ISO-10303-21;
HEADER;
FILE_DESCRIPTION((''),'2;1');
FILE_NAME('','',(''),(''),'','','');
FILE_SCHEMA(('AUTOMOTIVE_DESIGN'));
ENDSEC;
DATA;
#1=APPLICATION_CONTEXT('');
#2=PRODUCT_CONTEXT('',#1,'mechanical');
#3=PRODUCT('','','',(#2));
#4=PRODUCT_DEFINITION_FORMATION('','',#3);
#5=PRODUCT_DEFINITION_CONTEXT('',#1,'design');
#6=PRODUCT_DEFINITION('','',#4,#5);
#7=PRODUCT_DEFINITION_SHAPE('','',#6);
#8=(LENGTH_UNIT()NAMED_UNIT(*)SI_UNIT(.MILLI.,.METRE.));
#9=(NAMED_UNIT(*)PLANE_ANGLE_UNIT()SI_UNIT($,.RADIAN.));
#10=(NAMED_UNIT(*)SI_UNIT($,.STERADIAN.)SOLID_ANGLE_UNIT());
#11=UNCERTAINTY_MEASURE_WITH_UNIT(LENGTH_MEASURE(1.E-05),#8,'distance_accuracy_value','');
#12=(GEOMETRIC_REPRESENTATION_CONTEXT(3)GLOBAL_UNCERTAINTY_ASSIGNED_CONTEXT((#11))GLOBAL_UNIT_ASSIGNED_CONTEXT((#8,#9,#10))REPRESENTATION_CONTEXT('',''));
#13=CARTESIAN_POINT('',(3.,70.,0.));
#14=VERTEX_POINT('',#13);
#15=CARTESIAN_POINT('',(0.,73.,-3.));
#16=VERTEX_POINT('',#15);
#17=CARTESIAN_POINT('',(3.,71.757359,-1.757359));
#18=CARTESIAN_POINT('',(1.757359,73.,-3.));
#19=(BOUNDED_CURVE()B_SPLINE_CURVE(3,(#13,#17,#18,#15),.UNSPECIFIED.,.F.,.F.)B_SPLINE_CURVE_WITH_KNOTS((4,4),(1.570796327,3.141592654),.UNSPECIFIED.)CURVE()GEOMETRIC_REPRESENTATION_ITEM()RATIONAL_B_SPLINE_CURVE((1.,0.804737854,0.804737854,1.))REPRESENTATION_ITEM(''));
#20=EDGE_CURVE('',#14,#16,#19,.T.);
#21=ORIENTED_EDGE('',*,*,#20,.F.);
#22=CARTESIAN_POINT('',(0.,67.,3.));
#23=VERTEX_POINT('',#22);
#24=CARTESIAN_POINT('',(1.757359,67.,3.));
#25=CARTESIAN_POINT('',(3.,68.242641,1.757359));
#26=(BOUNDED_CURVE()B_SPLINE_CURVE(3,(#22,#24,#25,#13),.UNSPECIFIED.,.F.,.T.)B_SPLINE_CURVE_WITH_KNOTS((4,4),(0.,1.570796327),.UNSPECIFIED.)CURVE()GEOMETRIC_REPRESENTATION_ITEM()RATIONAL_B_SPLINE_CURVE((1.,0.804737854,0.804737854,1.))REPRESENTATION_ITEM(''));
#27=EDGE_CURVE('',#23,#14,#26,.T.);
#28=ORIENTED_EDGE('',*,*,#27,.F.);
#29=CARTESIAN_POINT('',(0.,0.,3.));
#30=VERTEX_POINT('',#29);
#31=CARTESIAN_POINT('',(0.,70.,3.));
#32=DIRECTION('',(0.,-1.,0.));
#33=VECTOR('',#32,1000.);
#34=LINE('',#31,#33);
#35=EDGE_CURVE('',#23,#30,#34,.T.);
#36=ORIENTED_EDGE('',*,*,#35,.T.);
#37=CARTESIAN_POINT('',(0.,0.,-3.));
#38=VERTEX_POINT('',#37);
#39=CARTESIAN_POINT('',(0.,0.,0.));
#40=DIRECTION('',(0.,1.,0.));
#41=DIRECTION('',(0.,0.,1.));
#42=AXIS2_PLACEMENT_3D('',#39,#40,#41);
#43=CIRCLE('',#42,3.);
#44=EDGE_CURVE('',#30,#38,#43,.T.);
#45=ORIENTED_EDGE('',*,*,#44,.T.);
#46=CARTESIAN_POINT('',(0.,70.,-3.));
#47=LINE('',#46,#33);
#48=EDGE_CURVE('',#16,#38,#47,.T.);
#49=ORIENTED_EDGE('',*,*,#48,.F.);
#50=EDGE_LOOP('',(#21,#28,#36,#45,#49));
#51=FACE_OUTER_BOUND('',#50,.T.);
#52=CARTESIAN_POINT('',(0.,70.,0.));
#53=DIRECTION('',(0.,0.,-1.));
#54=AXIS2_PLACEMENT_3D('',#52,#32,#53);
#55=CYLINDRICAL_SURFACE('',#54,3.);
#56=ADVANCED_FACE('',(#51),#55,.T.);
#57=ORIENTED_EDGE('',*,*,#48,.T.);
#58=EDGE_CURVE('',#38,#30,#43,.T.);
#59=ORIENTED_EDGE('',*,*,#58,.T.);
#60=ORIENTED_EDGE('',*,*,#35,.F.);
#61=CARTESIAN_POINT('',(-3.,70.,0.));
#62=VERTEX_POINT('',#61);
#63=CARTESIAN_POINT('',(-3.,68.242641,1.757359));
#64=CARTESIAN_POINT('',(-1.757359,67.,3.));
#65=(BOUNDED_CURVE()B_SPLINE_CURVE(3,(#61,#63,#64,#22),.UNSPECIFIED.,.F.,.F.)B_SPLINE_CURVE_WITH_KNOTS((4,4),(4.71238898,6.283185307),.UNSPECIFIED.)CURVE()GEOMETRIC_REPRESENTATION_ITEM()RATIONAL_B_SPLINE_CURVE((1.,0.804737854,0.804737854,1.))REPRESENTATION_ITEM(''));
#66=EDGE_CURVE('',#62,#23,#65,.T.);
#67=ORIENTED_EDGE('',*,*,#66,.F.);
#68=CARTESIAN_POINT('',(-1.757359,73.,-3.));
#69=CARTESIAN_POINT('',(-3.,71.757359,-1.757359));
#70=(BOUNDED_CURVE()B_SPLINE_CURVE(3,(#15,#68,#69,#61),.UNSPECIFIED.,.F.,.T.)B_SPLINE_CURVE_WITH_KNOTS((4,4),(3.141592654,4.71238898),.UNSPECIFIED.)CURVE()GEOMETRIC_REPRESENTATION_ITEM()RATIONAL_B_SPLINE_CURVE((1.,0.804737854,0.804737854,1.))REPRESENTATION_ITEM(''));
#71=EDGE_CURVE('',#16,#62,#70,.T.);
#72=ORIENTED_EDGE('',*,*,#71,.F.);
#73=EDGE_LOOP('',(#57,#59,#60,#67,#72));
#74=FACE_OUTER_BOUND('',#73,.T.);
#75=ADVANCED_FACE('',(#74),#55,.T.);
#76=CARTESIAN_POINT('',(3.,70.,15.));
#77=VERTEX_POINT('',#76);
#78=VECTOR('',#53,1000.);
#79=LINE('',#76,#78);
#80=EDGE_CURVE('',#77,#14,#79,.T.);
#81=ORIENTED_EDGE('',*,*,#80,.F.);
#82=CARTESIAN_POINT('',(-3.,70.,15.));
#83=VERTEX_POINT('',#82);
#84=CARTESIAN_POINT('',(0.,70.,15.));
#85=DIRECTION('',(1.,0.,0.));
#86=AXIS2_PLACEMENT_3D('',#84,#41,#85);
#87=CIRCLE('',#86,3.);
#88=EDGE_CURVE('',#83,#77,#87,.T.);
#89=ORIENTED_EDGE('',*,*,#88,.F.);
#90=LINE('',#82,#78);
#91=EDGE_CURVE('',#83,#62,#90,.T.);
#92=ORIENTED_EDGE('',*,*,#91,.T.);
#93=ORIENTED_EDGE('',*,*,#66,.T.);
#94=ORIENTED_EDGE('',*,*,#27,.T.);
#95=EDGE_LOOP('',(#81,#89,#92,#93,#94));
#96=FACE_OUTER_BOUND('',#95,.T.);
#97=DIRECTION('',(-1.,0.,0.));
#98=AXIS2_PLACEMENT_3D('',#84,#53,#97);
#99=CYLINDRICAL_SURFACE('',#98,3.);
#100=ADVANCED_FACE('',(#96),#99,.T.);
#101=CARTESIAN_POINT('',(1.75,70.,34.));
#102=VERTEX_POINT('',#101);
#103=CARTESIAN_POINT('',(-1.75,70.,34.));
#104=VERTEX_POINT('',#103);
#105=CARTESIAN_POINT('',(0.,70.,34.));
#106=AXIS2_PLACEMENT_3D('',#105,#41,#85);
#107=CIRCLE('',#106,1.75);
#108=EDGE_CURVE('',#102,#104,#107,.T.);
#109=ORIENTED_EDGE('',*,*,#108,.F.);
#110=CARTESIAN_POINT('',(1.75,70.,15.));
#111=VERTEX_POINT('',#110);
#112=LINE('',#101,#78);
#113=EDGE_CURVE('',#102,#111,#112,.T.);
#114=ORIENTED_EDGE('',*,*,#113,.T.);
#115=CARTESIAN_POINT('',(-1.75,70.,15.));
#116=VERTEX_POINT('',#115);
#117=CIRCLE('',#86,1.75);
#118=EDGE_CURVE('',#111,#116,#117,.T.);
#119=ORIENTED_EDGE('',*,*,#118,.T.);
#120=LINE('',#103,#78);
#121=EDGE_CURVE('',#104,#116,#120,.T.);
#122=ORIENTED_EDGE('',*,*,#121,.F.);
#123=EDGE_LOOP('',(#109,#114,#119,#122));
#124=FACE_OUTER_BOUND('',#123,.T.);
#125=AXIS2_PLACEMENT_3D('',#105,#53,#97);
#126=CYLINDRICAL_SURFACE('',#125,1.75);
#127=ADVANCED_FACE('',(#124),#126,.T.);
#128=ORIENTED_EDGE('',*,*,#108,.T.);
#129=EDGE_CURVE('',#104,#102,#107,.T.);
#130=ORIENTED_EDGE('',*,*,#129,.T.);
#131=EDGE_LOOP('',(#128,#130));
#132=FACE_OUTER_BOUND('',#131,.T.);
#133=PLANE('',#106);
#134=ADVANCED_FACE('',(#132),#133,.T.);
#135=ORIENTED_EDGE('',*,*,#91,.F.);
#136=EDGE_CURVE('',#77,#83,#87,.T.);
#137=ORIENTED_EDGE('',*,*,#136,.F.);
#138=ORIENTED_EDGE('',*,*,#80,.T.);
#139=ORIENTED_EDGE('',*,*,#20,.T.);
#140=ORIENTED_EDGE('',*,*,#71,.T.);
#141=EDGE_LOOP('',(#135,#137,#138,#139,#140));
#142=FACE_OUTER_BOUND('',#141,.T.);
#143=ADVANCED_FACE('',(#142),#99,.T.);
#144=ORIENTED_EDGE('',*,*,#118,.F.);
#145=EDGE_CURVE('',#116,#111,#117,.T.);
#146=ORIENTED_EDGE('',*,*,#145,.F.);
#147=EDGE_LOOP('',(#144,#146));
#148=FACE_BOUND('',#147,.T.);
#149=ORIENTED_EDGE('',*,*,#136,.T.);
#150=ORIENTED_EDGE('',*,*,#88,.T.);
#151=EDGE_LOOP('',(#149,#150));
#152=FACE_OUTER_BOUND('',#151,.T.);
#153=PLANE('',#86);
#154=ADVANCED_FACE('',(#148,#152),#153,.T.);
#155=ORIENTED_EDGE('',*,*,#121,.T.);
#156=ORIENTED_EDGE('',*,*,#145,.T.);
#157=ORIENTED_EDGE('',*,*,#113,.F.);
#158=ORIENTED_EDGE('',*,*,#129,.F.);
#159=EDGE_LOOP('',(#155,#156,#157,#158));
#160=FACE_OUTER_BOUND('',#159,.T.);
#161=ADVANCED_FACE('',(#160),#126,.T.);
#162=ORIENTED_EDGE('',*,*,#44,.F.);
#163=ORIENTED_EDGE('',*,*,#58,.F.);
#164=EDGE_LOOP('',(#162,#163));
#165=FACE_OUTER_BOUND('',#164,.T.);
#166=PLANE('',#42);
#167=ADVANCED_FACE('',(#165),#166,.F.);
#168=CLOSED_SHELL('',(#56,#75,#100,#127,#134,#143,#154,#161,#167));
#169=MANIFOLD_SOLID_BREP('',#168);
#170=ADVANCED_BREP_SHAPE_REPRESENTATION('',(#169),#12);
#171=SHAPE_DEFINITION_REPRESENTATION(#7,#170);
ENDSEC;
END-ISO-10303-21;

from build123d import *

# Parameters (mm, degrees)
SKETCH1_R           = 3
BOSS_EXTRUDE1_DEPTH = 70
SKETCH3_R           = 3
BOSS_EXTRUDE3_DEPTH = 15
BOSS_EXTRUDE4_DEPTH = 4
CUT_EXTRUDE1_DEPTH  = 77.216796049
SKETCH6_R           = 1.75
BOSS_EXTRUDE5_DEPTH = 19


with BuildPart() as part:
    # Sketch1 → Boss-Extrude1 (new body)
    with BuildSketch(Plane(origin=(0, 0, 0), x_dir=(1, 0, 0), z_dir=(0, 1, 0))):
        with Locations(Location((0, 0, 0), (0, 0, 270))):
            Circle(SKETCH1_R)
    extrude(amount=BOSS_EXTRUDE1_DEPTH)

    # Sketch3 → Boss-Extrude3 (add)
    with BuildSketch(Plane.XY):
        with Locations((0, 70)):
            Circle(SKETCH3_R)
    extrude(amount=BOSS_EXTRUDE3_DEPTH)

    # Sketch4 → Boss-Extrude4 (add)
    with BuildSketch(Plane(origin=(0, 70, 0), x_dir=(1, 0, 0), z_dir=(0, 1, 0))):
        with BuildLine():
            Line((-3, 0), (3, 0))
            ThreePointArc((3, 0), (0, 3), (-3, 0))
        make_face()
    extrude(amount=BOSS_EXTRUDE4_DEPTH)

    # Sketch5 → Cut-Extrude1 (cut, through all)
    with BuildSketch(Plane.XY.offset(15)):
        with BuildLine():
            Line((-3, 70), (-3, 74))
            Line((-3, 74), (3, 74))
            Line((3, 74), (3, 70))
            ThreePointArc((3, 70), (0, 73), (-3, 70))
        make_face()
    extrude(amount=-CUT_EXTRUDE1_DEPTH, mode=Mode.SUBTRACT)

    # Sketch6 → Boss-Extrude5 (add)
    with BuildSketch(Plane.XY.offset(15)):
        with Locations(Location((0, 70, 0), (0, 0, 180))):
            Circle(SKETCH6_R)
    extrude(amount=BOSS_EXTRUDE5_DEPTH)


solid = part.part
